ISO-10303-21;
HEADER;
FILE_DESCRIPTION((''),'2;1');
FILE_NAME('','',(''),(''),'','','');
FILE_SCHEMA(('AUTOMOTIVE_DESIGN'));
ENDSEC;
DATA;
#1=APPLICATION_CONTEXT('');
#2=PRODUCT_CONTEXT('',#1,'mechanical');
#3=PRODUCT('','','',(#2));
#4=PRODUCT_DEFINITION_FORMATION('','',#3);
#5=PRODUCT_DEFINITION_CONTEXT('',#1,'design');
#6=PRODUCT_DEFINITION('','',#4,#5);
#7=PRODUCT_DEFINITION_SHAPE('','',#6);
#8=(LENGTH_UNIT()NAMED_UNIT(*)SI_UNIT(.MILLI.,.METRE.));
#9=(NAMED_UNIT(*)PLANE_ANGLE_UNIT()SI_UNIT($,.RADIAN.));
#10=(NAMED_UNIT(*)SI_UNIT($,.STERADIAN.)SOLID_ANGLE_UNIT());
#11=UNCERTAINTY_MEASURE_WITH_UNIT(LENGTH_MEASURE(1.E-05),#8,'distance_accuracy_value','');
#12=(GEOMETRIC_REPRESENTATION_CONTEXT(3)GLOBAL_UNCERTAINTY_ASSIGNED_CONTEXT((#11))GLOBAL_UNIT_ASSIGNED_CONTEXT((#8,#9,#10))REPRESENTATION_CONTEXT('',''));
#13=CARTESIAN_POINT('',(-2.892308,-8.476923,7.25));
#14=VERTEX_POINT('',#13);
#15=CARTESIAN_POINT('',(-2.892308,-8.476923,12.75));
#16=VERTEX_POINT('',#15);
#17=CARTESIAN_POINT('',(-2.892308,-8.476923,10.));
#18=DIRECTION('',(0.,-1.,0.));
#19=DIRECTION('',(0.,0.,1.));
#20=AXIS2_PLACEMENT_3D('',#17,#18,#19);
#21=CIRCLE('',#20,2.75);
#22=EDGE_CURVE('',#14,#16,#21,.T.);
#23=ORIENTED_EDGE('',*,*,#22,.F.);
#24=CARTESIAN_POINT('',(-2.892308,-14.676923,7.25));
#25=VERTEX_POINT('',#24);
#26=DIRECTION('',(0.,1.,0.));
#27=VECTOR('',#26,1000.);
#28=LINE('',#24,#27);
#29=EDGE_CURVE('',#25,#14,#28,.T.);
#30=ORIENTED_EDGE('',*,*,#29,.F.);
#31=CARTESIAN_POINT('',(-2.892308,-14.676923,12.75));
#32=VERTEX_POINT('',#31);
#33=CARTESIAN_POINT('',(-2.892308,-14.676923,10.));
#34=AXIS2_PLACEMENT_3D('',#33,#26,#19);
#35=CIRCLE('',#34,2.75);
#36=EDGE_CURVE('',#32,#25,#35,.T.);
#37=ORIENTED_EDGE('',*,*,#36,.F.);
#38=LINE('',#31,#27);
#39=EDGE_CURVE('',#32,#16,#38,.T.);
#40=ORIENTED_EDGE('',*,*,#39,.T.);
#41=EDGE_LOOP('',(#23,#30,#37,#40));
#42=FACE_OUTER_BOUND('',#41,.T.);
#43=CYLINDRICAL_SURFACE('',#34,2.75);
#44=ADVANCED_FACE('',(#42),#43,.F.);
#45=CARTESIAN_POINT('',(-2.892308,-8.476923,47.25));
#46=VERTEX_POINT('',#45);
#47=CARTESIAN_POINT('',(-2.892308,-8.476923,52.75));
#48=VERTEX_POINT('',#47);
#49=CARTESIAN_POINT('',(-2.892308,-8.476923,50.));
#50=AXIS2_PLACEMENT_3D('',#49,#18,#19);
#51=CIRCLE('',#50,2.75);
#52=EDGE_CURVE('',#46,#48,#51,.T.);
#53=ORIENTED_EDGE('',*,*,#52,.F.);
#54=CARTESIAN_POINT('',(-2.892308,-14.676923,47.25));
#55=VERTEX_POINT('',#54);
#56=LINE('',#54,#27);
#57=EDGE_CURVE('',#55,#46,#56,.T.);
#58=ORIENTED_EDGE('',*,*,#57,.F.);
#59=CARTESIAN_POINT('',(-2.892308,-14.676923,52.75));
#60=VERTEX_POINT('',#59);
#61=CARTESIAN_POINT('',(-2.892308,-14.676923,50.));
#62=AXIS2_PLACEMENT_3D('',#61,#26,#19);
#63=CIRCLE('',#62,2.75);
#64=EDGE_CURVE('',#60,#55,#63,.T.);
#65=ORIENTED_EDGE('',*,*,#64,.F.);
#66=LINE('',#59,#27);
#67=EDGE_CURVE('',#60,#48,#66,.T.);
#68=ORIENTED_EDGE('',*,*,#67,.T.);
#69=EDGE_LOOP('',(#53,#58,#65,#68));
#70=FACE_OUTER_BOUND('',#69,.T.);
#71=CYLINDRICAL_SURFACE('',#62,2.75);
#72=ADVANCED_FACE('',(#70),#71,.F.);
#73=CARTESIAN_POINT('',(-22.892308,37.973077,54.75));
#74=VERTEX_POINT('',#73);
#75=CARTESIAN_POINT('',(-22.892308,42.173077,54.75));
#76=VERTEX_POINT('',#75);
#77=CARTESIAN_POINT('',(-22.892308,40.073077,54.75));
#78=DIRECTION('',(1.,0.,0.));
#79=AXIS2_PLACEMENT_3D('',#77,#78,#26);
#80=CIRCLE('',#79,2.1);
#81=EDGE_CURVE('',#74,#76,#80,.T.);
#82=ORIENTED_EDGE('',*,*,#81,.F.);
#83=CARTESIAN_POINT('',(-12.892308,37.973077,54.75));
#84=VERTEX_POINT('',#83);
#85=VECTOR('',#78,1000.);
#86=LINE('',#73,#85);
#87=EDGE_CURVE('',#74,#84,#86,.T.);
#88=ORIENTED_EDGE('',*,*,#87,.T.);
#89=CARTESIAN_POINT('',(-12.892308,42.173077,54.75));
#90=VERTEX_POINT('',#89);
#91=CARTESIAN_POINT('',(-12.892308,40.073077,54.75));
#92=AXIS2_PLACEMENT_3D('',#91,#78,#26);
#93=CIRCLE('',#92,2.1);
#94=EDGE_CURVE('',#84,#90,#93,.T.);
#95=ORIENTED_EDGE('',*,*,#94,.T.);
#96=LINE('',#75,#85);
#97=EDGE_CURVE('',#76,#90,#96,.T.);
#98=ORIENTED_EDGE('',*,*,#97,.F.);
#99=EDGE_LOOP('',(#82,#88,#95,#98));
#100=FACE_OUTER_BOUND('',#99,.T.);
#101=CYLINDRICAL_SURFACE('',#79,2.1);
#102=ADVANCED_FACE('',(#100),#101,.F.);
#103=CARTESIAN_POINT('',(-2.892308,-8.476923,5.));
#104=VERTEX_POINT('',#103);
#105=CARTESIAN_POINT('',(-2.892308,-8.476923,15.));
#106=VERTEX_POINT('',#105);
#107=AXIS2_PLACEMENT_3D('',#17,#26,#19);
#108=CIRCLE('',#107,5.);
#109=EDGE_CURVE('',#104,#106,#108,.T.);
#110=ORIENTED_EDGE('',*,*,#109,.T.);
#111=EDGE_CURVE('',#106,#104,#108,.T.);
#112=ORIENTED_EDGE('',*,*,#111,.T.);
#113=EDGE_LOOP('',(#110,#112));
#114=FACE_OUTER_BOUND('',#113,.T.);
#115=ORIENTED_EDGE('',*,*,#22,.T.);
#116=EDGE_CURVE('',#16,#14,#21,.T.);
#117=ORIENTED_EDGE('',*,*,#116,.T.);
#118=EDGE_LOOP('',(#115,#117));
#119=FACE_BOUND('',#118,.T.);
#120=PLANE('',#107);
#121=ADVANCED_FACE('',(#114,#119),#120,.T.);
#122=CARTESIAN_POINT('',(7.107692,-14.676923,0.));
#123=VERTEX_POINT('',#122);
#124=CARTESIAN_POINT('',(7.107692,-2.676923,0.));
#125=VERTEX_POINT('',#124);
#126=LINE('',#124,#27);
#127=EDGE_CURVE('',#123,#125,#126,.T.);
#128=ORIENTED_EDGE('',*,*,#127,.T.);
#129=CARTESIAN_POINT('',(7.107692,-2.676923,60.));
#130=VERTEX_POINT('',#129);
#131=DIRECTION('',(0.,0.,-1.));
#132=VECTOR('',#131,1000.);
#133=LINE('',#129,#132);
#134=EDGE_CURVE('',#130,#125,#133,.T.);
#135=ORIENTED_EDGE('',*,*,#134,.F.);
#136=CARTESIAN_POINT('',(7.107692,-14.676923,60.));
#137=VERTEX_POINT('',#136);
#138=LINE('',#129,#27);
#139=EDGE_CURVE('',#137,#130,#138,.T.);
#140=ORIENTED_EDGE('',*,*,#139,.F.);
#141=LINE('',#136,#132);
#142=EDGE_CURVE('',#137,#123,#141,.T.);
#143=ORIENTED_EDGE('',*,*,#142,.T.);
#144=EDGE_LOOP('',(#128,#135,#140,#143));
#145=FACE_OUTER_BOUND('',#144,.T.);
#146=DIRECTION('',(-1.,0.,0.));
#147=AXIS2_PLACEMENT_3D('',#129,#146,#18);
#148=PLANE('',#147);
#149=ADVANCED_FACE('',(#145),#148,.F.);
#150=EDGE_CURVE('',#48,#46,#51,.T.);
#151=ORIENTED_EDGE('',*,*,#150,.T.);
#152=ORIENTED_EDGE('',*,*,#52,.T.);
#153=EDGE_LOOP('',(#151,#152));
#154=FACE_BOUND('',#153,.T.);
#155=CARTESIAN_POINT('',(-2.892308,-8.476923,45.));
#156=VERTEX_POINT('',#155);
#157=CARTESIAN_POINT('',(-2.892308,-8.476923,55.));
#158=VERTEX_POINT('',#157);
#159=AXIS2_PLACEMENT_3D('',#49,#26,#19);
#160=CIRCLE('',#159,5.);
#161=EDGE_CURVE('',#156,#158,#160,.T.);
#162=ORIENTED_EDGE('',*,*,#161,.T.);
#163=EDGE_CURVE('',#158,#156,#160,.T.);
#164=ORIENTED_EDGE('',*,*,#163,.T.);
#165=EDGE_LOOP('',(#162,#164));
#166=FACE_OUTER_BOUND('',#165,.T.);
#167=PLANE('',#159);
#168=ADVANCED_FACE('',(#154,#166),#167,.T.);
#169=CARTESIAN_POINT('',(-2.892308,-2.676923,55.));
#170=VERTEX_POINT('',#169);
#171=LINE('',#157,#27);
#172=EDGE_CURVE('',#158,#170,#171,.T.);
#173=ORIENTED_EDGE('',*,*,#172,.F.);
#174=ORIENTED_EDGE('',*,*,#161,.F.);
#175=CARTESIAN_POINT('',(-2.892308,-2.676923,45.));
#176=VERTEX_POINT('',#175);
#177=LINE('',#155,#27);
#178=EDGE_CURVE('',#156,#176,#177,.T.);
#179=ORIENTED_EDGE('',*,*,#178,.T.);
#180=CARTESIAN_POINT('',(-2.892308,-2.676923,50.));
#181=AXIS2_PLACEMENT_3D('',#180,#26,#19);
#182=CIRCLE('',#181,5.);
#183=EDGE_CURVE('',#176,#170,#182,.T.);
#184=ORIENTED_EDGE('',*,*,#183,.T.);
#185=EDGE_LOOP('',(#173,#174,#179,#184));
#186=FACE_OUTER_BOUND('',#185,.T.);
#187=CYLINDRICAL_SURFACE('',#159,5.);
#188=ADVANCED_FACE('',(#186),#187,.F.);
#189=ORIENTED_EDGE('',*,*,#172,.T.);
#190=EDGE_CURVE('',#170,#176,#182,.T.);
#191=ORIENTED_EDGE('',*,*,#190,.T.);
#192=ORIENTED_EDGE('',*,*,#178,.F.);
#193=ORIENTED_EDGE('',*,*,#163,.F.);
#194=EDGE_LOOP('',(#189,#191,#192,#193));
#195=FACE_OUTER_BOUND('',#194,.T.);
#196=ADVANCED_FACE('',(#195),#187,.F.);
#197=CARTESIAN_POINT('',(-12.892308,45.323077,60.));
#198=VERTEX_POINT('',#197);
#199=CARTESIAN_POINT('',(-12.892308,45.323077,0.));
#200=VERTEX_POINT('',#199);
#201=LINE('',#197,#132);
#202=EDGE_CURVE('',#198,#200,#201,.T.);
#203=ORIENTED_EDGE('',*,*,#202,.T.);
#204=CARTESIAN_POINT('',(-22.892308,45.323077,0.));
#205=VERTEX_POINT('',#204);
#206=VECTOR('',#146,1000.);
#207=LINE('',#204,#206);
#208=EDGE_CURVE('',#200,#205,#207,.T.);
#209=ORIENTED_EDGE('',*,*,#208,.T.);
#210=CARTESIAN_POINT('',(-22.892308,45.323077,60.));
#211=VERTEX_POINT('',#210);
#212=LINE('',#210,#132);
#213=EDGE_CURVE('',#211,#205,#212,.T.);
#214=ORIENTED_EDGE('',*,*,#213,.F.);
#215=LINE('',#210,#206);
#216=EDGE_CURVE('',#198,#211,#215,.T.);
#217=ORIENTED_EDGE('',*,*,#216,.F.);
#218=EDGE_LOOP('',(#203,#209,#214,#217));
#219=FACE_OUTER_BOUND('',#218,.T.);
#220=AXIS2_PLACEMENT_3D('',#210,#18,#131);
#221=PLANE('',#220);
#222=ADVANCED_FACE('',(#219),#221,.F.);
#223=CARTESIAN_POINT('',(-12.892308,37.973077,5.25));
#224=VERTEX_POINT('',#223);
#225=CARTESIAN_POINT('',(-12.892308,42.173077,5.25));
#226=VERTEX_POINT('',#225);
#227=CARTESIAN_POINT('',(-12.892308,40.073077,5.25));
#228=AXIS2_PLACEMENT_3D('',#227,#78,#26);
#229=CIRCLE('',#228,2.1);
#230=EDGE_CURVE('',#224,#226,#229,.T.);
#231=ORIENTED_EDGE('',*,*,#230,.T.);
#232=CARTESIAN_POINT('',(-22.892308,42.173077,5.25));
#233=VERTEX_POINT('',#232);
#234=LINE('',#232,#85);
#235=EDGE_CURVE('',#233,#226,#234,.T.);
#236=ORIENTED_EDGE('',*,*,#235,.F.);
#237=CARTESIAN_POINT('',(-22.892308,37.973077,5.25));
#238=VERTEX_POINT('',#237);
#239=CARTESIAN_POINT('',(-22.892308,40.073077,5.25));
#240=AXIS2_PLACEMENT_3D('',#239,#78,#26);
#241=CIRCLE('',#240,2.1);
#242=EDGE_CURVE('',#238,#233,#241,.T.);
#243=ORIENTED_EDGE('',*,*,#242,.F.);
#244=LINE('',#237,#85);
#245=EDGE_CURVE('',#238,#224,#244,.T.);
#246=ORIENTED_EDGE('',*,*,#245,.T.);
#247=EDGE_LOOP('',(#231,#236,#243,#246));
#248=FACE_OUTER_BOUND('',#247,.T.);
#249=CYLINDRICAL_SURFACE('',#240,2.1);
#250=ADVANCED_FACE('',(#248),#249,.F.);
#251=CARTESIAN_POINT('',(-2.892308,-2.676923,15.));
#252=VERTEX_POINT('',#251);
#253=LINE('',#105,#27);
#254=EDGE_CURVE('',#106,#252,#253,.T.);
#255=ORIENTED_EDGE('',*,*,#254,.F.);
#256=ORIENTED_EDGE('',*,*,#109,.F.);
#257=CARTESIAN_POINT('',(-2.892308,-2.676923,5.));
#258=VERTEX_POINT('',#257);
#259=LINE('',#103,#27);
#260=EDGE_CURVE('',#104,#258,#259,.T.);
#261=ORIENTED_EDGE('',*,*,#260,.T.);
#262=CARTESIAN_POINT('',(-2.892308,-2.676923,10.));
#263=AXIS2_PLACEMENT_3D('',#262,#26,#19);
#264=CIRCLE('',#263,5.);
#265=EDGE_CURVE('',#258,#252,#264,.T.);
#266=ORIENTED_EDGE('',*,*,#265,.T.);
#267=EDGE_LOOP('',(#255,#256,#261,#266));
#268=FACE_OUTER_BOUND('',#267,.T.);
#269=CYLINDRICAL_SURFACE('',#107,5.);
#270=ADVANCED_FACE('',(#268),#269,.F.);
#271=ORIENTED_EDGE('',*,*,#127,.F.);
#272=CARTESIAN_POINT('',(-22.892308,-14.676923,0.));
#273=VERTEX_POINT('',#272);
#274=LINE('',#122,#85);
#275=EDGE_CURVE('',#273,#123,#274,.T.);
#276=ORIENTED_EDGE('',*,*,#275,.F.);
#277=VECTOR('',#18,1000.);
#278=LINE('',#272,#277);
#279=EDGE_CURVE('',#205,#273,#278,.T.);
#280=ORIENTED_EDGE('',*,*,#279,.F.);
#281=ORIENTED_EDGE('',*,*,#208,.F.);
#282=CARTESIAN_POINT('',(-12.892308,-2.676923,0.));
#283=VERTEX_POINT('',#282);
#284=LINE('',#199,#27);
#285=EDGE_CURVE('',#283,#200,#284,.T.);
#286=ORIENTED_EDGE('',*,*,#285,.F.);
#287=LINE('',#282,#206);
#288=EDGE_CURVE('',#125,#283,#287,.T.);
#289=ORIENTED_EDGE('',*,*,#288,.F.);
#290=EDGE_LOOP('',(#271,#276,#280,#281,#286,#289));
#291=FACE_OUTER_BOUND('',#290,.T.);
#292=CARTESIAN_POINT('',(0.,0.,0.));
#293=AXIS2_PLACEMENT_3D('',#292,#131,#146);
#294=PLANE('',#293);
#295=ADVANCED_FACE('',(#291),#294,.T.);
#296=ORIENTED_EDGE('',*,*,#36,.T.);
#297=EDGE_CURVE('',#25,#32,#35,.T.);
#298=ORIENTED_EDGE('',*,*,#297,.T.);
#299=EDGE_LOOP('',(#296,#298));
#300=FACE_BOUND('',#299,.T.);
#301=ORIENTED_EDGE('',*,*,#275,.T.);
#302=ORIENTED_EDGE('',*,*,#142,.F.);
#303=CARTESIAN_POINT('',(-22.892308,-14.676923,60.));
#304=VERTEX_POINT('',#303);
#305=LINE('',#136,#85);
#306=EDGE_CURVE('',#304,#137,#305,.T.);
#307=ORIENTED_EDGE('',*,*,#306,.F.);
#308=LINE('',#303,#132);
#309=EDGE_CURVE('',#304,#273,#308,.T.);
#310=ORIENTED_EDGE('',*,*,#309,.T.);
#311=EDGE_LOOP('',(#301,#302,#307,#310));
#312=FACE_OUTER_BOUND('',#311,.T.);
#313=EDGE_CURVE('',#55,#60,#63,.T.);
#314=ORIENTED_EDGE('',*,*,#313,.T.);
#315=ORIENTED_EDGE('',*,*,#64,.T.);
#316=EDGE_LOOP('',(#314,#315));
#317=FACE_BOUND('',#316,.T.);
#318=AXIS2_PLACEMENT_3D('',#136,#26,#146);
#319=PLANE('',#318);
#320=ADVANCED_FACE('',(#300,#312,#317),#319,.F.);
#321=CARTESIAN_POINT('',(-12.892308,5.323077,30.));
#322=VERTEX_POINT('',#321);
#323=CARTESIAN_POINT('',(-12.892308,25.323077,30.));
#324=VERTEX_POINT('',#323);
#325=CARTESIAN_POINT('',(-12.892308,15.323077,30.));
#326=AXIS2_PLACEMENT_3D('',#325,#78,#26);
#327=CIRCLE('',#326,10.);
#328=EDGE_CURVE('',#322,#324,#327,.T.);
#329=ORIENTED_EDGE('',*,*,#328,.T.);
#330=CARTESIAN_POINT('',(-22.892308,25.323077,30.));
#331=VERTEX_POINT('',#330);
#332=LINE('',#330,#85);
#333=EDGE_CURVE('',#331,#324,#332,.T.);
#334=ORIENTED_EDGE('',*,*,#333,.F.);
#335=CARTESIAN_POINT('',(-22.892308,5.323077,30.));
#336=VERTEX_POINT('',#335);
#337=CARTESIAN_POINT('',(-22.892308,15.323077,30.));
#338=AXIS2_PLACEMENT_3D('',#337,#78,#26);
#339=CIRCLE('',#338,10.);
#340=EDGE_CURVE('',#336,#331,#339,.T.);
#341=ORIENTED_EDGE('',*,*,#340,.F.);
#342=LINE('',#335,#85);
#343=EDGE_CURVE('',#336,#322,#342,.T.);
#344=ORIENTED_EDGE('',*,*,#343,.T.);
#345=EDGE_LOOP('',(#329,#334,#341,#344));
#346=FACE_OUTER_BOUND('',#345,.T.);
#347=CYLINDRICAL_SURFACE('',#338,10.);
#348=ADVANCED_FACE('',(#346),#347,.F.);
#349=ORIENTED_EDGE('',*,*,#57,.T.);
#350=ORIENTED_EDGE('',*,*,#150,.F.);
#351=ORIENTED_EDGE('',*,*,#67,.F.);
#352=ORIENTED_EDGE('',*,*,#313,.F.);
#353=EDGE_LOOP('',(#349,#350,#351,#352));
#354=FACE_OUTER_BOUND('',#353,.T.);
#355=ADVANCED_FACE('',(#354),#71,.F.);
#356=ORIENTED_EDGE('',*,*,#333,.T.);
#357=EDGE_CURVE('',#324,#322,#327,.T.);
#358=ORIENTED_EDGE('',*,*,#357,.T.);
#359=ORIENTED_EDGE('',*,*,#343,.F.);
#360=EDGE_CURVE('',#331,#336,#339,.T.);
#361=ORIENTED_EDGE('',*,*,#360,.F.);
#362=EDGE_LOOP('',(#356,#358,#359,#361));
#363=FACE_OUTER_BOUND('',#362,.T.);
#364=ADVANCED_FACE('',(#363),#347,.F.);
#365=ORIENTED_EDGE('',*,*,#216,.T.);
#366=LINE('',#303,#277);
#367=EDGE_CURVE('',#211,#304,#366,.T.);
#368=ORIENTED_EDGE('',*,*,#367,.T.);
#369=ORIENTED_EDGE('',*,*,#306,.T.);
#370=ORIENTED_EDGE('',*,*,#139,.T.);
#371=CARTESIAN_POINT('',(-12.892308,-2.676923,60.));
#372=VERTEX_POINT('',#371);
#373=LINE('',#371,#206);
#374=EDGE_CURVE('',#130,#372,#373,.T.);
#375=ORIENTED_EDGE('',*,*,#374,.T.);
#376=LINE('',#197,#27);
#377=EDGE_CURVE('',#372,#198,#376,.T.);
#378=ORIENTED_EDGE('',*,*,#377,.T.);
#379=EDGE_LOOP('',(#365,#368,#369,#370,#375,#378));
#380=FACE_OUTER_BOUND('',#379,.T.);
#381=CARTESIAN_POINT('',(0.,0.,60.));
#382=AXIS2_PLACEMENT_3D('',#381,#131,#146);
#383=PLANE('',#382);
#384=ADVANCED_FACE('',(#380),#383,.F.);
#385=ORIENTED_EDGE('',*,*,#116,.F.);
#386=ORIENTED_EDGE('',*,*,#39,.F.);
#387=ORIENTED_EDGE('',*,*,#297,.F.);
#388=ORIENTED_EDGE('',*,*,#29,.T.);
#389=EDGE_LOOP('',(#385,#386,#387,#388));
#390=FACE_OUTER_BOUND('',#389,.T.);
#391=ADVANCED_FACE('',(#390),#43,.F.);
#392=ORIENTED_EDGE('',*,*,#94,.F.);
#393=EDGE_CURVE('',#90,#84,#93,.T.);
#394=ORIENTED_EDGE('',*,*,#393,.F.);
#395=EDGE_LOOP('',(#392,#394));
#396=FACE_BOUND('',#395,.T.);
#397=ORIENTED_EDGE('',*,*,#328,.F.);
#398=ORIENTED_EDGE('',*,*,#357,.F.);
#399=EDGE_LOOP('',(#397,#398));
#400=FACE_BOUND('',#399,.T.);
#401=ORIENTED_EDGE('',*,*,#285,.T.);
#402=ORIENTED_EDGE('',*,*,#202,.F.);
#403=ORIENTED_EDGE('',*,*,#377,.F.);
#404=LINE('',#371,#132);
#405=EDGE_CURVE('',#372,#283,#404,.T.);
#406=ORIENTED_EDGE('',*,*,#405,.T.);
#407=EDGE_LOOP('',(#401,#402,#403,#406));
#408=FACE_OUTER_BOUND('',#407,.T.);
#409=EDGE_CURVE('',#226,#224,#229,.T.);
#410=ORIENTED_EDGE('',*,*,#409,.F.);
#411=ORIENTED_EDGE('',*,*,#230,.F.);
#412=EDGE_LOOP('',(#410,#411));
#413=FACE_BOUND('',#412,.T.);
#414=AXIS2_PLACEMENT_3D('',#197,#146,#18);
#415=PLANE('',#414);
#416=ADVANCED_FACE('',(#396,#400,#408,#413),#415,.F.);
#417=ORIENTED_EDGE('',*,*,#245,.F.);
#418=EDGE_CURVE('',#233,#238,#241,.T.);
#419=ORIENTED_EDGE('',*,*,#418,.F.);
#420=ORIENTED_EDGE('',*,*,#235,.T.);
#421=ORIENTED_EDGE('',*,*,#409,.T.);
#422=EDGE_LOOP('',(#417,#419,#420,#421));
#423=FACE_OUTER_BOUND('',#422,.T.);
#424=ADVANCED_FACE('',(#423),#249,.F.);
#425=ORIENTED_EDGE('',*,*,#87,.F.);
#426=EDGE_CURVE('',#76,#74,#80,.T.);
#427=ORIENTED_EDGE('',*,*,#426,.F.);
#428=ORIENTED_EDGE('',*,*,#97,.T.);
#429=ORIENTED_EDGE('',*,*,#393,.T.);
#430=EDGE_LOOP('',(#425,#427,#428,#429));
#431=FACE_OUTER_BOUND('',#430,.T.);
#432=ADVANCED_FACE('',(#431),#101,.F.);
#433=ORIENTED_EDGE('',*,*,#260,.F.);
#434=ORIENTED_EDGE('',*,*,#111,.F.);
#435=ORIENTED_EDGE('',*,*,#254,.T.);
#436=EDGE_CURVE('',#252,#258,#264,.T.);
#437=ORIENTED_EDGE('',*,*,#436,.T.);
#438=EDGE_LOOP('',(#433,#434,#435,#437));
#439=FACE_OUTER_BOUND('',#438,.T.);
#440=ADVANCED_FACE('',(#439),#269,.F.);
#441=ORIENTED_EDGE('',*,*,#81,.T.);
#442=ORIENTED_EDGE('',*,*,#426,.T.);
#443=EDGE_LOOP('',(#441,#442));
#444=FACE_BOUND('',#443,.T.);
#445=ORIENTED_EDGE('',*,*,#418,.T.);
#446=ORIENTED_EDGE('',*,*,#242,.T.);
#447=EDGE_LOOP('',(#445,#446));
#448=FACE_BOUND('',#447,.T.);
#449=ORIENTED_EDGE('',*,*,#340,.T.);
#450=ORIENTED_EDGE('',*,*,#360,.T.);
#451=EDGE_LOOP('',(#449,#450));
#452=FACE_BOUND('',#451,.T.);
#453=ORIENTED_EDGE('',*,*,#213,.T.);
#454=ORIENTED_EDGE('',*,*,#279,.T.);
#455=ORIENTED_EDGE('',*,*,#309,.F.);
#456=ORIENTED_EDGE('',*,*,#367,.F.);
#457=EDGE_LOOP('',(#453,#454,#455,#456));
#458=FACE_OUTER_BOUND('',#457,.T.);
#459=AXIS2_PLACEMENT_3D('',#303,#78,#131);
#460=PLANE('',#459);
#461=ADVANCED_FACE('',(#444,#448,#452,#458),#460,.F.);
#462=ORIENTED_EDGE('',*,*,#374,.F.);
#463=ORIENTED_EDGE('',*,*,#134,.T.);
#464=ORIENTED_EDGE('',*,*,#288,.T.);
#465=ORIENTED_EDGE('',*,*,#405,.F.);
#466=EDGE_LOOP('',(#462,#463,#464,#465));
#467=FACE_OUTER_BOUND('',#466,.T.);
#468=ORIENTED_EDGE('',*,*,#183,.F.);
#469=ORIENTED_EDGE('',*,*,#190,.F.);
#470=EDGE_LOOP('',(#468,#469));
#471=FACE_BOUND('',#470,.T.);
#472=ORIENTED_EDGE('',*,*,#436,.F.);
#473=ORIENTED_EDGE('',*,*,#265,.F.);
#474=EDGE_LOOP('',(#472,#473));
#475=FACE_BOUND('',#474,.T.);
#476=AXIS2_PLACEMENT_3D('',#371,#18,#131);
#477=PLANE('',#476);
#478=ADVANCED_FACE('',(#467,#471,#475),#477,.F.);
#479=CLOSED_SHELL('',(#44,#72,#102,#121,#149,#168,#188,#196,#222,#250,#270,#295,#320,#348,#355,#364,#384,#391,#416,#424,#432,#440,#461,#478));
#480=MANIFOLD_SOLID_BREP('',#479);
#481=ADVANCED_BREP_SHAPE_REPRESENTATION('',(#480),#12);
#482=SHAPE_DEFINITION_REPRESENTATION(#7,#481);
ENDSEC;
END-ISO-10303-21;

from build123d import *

# Parameters (mm, degrees)
EXTRUDE_1_DEPTH     = 60
SKETCH_2_R          = 10
CUT_EXTRUDE_1_DEPTH = 78.808619714
SKETCH_3_R          = 2.1
CUT_EXTRUDE_2_DEPTH = 78.808619714
SKETCH_4_R          = 2.75
CUT_EXTRUDE_3_DEPTH = 81.17516917
SKETCH_5_R          = 5
CUT_EXTRUDE_4_DEPTH = 5.8


with BuildPart() as part:
    # 草图1 → 凸台-拉伸1 (new body)
    with BuildSketch(Plane.XY):
        Polygon((-12.892307692, 45.323076923), (-12.892307692, -2.676923077), (7.107692308, -2.676923077), (7.107692308, -14.676923077), (-22.892307692, -14.676923077), (-22.892307692, 45.323076923), align=None)
    extrude(amount=EXTRUDE_1_DEPTH)

    # 草图2 → 切除-拉伸1 (cut, through all)
    with BuildSketch(Plane(origin=(-12.892307692, 0, 0), x_dir=(0, 0, -1), z_dir=(1, 0, 0))):
        with Locations(Location((-30, 15.323076923, 0), (0, 0, 90))):
            Circle(SKETCH_2_R)
    extrude(amount=-CUT_EXTRUDE_1_DEPTH, mode=Mode.SUBTRACT)

    # 草图3 → 切除-拉伸2 (cut, through all)
    with BuildSketch(Plane(origin=(-12.892307692, 0, 0), x_dir=(0, 0, -1), z_dir=(1, 0, 0))):
        with Locations(Location((-54.75, 40.073076923, 0), (0, 0, 90))):
            Circle(SKETCH_3_R)
        with Locations(Location((-5.25, 40.073076923, 0), (0, 0, 90))):
            Circle(SKETCH_3_R)
    extrude(amount=-CUT_EXTRUDE_2_DEPTH, mode=Mode.SUBTRACT)

    # 草图4 → 切除-拉伸3 (cut, through all)
    with BuildSketch(Plane(origin=(0, -2.676923077, 0), x_dir=(1, 0, 0), z_dir=(0, 1, 0))):
        with Locations(Location((-2.892307692, -10, 0), (0, 0, 270))):
            Circle(SKETCH_4_R)
        with Locations(Location((-2.892307692, -50, 0), (0, 0, 270))):
            Circle(SKETCH_4_R)
    extrude(amount=-CUT_EXTRUDE_3_DEPTH, mode=Mode.SUBTRACT)

    # 草图5 → 切除-拉伸4 (cut)
    with BuildSketch(Plane(origin=(0, -2.676923077, 0), x_dir=(1, 0, 0), z_dir=(0, 1, 0))):
        with Locations(Location((-2.892307692, -10, 0), (0, 0, 270))):
            Circle(SKETCH_5_R)
        with Locations(Location((-2.892307692, -50, 0), (0, 0, 270))):
            Circle(SKETCH_5_R)
    extrude(amount=-CUT_EXTRUDE_4_DEPTH, mode=Mode.SUBTRACT)


solid = part.part
